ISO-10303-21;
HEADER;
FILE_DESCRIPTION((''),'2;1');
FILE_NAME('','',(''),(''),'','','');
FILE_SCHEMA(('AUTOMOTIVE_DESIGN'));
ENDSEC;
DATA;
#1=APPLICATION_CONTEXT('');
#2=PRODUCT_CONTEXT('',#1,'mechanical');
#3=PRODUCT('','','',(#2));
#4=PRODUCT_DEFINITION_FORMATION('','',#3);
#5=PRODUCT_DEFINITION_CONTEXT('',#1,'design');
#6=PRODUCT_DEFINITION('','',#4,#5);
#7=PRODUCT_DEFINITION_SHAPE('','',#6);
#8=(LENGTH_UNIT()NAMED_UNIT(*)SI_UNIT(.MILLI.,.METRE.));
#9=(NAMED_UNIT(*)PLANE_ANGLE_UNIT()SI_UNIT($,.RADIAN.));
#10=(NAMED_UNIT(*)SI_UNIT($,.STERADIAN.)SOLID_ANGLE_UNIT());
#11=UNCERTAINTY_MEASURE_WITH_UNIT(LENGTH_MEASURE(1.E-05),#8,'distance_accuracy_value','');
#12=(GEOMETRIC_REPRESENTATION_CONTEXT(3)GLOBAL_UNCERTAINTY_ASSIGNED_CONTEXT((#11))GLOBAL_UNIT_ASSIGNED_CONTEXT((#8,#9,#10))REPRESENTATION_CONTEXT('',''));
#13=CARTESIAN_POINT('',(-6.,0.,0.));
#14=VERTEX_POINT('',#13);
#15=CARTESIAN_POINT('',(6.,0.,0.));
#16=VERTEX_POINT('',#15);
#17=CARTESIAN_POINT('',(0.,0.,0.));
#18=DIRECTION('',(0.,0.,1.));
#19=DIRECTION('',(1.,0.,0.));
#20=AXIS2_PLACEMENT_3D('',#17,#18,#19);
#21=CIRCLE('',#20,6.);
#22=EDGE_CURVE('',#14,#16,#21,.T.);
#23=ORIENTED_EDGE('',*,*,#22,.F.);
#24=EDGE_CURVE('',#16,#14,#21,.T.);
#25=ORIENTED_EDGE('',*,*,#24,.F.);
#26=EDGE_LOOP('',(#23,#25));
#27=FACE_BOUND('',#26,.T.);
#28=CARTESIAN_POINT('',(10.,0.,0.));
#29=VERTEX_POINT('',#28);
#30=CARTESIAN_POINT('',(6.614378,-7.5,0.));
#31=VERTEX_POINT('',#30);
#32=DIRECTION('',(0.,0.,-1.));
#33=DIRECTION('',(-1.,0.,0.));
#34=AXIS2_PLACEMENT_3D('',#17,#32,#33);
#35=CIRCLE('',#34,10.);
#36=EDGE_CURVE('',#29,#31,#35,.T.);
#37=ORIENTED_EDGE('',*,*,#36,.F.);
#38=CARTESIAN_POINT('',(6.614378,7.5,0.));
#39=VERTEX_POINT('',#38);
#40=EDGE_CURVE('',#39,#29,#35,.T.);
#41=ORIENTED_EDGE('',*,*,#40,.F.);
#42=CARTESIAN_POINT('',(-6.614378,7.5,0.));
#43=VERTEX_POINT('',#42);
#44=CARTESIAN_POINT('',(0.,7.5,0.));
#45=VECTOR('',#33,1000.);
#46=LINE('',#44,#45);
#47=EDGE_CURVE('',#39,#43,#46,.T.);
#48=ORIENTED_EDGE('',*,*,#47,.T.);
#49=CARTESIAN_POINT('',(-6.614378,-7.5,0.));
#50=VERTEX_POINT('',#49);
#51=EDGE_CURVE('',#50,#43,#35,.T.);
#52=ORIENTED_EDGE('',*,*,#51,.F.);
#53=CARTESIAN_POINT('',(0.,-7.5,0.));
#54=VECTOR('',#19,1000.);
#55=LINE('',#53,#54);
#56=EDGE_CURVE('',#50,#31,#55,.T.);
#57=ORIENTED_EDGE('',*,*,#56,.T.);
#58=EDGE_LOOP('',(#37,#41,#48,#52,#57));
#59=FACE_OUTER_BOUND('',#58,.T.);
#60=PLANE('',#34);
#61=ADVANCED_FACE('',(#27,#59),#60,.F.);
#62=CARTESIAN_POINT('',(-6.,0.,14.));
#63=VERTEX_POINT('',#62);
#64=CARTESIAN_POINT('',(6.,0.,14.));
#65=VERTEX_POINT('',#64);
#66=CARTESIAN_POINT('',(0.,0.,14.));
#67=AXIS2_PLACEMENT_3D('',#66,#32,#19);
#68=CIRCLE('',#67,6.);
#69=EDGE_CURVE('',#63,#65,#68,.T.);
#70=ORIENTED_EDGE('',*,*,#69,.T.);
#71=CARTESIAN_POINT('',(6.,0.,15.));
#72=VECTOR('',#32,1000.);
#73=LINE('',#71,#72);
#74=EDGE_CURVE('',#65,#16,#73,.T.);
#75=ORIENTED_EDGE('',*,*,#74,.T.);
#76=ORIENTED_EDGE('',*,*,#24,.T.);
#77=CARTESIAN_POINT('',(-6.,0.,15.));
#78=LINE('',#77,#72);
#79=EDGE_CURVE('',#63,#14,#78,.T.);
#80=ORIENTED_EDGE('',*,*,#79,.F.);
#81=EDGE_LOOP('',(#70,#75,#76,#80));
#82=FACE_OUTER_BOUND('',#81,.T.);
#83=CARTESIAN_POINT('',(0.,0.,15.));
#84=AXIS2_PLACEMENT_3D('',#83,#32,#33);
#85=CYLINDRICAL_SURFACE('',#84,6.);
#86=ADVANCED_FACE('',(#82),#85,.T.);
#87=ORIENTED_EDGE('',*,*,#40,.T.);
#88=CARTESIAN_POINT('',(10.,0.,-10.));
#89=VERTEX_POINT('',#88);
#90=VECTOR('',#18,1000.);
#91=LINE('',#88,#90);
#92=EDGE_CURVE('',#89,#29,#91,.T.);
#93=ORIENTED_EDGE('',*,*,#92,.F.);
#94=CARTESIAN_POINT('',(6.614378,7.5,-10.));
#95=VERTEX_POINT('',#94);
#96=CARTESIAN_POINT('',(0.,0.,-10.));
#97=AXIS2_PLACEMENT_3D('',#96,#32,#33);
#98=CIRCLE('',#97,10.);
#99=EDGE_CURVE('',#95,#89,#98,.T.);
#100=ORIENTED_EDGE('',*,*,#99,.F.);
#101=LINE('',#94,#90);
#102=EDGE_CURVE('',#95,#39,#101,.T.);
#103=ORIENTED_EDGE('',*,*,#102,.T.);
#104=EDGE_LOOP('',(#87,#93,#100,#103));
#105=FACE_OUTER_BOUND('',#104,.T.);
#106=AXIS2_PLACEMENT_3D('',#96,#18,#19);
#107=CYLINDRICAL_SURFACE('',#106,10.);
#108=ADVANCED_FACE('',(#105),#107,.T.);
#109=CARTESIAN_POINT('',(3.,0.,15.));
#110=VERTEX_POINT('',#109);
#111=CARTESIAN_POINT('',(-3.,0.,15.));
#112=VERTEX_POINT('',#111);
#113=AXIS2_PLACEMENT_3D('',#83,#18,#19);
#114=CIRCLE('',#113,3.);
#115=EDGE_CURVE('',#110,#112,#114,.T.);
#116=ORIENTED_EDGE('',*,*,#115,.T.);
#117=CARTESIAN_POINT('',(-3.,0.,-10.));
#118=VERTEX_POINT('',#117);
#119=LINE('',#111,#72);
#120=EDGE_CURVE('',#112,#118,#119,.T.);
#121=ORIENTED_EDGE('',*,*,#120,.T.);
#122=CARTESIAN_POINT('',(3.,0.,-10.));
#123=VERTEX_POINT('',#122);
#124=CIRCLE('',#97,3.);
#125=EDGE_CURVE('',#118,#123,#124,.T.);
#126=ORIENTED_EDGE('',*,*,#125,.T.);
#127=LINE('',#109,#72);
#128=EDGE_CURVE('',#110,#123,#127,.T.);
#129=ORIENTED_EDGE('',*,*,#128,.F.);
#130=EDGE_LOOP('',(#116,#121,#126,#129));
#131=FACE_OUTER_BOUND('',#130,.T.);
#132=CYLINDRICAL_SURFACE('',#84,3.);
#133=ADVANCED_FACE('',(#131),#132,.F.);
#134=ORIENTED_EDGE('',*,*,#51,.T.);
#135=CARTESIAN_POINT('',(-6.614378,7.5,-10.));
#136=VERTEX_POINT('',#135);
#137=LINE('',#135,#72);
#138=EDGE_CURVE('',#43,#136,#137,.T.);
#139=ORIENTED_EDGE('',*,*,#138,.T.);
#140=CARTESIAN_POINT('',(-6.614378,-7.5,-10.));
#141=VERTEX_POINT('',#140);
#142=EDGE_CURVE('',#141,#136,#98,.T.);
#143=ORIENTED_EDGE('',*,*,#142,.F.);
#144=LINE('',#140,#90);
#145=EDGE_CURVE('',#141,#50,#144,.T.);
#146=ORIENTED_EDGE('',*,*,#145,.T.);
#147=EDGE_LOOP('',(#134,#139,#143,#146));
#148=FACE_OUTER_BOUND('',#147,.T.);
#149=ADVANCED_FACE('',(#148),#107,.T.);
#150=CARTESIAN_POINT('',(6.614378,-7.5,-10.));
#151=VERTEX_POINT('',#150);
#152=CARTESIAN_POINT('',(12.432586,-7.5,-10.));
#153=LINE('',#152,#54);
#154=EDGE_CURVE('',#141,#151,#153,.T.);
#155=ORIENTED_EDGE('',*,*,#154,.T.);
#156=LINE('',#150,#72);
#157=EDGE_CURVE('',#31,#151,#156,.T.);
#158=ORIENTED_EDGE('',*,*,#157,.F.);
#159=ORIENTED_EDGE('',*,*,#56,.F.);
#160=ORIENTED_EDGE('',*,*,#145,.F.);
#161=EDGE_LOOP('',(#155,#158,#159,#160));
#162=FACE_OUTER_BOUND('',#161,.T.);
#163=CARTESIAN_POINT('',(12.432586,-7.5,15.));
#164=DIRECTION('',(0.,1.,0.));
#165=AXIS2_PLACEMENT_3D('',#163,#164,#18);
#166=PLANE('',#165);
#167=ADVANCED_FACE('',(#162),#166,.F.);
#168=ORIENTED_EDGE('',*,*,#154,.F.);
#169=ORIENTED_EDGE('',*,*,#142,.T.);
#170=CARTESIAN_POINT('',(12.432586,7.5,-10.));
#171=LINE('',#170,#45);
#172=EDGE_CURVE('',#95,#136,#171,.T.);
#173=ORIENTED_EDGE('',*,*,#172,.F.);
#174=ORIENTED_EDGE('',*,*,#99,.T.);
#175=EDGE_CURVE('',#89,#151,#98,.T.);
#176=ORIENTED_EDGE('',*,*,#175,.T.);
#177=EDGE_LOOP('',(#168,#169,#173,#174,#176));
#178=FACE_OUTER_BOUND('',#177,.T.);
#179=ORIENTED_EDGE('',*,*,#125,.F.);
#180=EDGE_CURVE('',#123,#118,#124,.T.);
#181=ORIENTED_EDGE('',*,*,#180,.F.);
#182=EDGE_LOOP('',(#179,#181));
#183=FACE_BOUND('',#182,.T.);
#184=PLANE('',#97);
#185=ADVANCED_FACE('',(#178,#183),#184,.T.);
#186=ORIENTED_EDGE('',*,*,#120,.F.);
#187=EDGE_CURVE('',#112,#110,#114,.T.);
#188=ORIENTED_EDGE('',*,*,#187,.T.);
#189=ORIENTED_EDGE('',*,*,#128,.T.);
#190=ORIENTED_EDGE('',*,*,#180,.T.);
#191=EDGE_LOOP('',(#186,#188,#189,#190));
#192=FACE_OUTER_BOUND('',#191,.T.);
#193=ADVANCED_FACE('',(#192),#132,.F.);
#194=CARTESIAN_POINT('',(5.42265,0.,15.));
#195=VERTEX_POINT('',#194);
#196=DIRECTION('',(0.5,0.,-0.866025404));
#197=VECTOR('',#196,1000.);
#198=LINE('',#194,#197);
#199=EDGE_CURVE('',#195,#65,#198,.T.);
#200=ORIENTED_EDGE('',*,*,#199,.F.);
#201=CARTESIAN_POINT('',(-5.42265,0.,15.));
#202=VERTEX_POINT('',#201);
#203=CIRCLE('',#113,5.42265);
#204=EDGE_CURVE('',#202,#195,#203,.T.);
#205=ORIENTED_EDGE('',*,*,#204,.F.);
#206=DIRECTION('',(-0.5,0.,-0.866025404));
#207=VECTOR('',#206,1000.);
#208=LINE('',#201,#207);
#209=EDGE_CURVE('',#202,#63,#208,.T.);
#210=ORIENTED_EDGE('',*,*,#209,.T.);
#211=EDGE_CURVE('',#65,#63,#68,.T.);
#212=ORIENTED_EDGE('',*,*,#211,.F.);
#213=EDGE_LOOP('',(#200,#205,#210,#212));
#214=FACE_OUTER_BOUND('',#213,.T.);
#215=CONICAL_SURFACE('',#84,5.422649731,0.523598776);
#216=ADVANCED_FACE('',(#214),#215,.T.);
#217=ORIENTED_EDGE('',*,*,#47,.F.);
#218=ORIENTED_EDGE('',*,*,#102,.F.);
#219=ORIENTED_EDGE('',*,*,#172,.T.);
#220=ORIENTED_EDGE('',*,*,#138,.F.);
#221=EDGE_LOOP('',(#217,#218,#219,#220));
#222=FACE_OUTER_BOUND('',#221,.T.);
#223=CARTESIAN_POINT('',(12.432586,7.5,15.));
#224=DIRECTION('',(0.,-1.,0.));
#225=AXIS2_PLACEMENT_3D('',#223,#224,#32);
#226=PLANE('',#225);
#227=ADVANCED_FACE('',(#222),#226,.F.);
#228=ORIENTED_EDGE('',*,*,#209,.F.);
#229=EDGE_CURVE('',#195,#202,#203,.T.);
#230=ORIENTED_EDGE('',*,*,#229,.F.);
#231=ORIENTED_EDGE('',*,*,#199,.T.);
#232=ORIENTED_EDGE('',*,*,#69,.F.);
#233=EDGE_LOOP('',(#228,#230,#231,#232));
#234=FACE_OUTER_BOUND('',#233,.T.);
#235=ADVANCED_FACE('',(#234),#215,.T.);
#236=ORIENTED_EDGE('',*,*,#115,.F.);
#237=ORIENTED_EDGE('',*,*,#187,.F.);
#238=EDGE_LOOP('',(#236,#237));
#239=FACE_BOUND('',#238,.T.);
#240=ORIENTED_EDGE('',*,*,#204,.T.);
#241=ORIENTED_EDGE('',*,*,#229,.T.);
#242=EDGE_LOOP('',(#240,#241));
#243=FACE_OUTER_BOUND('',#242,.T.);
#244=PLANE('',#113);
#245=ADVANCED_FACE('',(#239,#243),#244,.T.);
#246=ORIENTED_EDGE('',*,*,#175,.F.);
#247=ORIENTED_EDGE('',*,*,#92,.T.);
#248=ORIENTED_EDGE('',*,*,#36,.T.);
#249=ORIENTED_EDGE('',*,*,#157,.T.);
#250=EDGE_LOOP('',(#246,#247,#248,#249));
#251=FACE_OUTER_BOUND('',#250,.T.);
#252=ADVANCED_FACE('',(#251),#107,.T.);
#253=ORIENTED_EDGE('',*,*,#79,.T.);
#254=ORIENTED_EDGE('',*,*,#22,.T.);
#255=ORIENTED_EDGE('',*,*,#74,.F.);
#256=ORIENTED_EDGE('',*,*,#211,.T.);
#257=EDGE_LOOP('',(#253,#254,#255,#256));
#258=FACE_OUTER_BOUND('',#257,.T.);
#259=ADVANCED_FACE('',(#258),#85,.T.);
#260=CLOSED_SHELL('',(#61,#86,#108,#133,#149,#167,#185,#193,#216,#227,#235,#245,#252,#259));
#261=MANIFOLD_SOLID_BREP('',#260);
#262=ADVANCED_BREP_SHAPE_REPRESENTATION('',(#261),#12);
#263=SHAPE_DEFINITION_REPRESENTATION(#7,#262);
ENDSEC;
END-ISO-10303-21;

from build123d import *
from build123d.topology import SkipClean

# Parameters (mm, degrees)
SKETCH1_R           = 6
SKETCH1_R_2         = 3
BOSS_EXTRUDE1_DEPTH = 15
CHAMFER1_SIZE       = 1
CHAMFER1_SIZE2      = 0.577350269
BOSS_EXTRUDE2_START = 10
SKETCH2_R           = 10
SKETCH2_R_2         = 3
BOSS_EXTRUDE2_DEPTH = 10
CUT_EXTRUDE1_DEPTH  = 29.722813233


with BuildPart() as part:
    # Sketch1 → Boss-Extrude1 (new body)
    with BuildSketch(Plane.XY):
        Circle(SKETCH1_R)
        Circle(SKETCH1_R_2, mode=Mode.SUBTRACT)
    extrude(amount=BOSS_EXTRUDE1_DEPTH)

    # Chamfer1
    chamfer1_edges = [part.edges().sort_by_distance(p)[0] for p in [
        (-6, 0, 15),
    ]]
    chamfer1_side = [part.faces().sort_by_distance(p)[0] for p in [
        (-6, 0, 7.5),
    ]]
    chamfer(chamfer1_edges, length=CHAMFER1_SIZE, length2=CHAMFER1_SIZE2, reference=chamfer1_side[0])

    # Sketch2 → Boss-Extrude2 (add)
    with SkipClean():  # the faces are left unmerged after this step: merging them gives an invalid solid
        with BuildSketch(Plane(origin=(0, 0, 0), x_dir=(-1, 0, 0), z_dir=(0, 0, -1)).offset(BOSS_EXTRUDE2_START)):
            Circle(SKETCH2_R)
            Circle(SKETCH2_R_2, mode=Mode.SUBTRACT)
        extrude(amount=-BOSS_EXTRUDE2_DEPTH)

    # Sketch3 → Cut-Extrude1 (cut, through all)
    with SkipClean():  # the faces are left unmerged after this step: merging them gives an invalid solid
        with BuildSketch(Plane(origin=(0, 0, -10), x_dir=(-1, 0, 0), z_dir=(0, 0, -1))):
            Polygon((-12.432586445, 7.5), (-12.432586445, 16.991345965), (16.514398983, 13.775765777), (12.432586445, 7.5), align=None)
            Polygon((-12.432586445, -7.5), (12.432586445, -7.5), (9.879584392, -18.980106847), (-12.432586445, -18.242292142), align=None)
        extrude(amount=-CUT_EXTRUDE1_DEPTH, mode=Mode.SUBTRACT)


solid = part.part
